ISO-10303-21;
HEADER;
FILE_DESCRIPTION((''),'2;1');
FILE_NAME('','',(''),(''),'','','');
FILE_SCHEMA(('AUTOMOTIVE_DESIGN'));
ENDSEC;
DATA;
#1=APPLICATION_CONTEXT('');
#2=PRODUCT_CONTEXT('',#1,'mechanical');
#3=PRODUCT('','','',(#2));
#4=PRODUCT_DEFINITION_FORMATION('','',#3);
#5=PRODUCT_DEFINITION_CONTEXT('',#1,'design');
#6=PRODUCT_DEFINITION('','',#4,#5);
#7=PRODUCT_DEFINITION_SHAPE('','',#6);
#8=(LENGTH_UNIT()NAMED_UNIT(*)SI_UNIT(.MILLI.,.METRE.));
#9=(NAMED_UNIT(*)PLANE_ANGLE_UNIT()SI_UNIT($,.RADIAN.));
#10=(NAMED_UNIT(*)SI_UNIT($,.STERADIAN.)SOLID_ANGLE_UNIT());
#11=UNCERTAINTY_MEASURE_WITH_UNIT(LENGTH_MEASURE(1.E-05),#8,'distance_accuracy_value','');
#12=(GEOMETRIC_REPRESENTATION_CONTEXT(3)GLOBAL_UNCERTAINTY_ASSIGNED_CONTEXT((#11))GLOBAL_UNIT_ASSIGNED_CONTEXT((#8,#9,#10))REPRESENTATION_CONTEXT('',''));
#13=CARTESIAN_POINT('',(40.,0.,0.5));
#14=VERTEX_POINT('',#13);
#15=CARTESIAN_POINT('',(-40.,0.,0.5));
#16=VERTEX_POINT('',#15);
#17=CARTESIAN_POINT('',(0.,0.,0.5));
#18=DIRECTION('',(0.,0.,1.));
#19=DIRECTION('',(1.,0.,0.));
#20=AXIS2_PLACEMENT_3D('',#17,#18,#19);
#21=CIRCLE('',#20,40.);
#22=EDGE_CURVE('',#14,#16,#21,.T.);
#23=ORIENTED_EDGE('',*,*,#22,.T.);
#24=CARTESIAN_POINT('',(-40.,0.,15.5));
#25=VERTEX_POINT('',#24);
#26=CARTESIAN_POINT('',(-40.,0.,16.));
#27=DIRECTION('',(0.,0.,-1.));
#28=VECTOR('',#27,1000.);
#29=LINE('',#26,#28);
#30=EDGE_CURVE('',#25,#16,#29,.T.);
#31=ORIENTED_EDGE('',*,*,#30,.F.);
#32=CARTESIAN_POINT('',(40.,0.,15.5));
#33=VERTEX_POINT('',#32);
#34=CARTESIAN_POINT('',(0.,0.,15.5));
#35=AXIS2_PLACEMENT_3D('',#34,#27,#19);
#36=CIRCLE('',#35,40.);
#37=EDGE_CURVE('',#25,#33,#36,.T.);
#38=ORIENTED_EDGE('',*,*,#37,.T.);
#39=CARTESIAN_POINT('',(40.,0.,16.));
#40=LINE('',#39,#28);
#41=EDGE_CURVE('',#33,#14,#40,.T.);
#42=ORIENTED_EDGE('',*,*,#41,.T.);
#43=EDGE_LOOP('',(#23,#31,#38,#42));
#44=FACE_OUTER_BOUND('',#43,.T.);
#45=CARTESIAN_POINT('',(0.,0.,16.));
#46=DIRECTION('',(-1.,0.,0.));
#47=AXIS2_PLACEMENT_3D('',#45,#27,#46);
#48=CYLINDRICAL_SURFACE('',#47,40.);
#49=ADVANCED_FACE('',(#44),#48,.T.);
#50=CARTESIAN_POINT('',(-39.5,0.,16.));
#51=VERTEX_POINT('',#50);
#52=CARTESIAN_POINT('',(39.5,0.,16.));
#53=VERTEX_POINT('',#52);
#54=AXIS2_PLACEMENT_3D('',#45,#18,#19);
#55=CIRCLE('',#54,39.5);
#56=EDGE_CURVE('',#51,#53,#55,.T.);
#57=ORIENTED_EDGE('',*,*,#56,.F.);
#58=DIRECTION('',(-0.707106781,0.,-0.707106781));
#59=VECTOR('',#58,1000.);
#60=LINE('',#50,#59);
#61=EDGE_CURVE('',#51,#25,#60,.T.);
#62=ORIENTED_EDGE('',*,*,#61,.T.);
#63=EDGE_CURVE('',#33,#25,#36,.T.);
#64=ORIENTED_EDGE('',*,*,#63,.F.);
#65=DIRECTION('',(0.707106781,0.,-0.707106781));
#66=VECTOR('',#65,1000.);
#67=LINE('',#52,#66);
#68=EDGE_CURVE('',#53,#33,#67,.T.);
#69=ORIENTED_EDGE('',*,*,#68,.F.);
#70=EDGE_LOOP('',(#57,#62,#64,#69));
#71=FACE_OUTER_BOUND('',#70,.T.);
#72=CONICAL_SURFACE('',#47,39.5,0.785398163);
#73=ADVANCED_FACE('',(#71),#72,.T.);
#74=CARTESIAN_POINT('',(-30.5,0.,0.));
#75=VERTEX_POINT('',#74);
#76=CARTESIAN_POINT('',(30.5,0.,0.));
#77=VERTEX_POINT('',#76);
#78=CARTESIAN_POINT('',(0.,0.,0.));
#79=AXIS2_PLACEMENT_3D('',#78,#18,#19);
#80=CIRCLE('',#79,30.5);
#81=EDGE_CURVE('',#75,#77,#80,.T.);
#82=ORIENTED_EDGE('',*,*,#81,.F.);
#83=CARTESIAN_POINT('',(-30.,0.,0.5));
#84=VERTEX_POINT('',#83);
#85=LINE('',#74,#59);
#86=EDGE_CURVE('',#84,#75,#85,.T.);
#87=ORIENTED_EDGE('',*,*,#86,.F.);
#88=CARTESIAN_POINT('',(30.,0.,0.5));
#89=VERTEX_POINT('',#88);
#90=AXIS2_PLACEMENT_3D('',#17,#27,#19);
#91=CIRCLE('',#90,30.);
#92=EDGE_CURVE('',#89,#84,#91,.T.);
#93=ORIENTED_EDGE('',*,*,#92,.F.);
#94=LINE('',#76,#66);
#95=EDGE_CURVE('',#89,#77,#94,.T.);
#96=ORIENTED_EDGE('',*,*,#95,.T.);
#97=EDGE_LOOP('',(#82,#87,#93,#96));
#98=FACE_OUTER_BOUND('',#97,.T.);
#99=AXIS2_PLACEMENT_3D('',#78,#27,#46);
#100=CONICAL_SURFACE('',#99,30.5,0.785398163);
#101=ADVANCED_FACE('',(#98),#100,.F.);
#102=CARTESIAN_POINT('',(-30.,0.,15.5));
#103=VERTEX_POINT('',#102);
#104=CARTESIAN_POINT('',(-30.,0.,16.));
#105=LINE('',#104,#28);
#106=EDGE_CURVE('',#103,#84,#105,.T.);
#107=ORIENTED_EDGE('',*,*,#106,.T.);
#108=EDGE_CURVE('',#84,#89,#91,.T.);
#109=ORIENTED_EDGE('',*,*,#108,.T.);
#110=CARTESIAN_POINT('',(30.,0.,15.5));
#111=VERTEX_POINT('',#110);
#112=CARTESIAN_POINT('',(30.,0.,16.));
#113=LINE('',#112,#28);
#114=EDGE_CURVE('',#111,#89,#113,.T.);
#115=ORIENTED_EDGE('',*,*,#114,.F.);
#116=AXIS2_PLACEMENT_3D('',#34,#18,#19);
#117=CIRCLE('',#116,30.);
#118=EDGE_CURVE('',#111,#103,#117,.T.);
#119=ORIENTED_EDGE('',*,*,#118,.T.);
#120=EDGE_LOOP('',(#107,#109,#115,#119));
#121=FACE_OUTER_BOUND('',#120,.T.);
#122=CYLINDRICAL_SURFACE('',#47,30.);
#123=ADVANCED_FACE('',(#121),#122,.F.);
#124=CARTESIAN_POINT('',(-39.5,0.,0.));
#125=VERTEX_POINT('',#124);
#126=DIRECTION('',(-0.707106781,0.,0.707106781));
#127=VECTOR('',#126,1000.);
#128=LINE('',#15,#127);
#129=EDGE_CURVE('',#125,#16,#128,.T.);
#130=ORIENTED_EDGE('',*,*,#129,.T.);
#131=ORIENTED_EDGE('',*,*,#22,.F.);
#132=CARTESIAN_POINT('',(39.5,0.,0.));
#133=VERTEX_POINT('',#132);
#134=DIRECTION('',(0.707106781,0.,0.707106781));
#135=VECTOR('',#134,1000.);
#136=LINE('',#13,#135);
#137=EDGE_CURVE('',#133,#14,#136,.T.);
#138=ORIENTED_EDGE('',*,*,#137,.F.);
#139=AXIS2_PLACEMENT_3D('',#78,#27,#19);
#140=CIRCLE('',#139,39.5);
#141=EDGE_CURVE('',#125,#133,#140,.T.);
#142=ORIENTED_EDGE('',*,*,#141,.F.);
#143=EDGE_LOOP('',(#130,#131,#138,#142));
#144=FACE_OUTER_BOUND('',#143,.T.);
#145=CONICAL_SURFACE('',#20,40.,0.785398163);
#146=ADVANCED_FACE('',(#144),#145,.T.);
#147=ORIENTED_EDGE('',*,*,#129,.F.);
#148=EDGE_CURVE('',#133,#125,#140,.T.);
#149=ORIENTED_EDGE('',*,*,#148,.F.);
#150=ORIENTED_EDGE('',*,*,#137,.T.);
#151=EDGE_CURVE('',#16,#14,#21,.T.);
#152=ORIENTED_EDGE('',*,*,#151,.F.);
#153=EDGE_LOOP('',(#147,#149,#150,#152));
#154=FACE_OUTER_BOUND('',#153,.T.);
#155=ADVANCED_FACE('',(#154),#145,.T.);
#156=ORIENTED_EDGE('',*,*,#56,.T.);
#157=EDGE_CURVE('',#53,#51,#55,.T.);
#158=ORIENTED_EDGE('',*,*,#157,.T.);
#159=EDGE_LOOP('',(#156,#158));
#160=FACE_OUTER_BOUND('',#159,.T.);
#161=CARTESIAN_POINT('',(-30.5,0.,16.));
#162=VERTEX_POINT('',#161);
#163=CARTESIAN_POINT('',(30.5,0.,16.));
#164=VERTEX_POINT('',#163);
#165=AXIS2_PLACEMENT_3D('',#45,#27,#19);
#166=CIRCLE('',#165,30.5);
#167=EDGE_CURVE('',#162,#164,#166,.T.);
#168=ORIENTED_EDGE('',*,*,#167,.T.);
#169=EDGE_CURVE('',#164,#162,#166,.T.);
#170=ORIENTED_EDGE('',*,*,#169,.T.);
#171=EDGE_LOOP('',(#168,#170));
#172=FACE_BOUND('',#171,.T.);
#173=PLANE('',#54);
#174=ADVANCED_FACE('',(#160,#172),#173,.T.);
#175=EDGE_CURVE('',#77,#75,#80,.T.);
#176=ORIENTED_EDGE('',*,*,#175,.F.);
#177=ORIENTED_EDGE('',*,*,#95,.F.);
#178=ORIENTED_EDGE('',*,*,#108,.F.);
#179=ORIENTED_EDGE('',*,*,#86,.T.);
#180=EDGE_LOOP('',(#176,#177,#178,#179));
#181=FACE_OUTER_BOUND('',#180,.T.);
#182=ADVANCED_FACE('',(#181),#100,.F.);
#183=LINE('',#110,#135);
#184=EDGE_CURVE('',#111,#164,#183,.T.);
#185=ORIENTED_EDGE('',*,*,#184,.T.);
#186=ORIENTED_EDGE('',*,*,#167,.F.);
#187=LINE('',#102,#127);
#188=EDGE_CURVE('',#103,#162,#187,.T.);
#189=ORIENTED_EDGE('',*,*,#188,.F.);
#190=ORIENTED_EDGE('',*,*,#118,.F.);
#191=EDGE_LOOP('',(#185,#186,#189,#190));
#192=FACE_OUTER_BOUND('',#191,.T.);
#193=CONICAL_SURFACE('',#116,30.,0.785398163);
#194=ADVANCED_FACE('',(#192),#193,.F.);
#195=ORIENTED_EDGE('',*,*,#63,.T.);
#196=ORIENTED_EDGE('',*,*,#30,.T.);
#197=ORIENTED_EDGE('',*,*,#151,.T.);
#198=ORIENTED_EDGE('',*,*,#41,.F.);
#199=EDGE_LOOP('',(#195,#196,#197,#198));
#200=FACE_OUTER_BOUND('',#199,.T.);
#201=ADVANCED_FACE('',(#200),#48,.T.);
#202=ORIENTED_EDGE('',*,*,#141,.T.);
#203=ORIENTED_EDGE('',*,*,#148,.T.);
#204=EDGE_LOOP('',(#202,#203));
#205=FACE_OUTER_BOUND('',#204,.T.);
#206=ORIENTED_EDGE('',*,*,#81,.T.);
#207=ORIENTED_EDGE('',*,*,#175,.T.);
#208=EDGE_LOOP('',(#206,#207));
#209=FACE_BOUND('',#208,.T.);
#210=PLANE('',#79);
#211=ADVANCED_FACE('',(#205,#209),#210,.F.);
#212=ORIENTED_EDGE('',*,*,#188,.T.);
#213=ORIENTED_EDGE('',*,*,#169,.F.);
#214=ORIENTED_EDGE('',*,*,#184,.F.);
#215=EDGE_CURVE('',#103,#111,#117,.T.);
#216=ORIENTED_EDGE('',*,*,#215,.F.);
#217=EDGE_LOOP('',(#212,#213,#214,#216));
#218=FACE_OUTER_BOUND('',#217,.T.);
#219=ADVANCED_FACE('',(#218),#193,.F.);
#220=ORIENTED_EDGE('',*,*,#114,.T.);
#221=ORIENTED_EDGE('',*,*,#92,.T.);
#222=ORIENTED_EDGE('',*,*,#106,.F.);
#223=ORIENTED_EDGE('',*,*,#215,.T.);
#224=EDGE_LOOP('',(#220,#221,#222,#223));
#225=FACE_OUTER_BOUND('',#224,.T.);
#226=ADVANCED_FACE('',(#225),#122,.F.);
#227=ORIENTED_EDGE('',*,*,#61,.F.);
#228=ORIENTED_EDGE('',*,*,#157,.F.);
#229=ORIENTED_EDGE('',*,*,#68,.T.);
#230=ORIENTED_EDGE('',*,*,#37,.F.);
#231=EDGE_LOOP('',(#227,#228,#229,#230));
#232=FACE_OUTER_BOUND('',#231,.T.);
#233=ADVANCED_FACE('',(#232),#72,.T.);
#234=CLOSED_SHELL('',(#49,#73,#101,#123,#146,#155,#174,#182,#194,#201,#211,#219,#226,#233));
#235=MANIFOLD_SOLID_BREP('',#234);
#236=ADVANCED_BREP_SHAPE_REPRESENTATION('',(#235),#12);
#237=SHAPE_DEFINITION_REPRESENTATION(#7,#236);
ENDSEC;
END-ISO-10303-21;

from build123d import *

# Parameters (mm, degrees)
SKETCH1_R           = 40
SKETCH1_R_2         = 30
BOSS_EXTRUDE1_DEPTH = 16
CHAMFER1_SIZE       = 0.5


with BuildPart() as part:
    # Sketch1 → Boss-Extrude1 (new body)
    with BuildSketch(Plane.XY):
        Circle(SKETCH1_R)
        Circle(SKETCH1_R_2, mode=Mode.SUBTRACT)
    extrude(amount=BOSS_EXTRUDE1_DEPTH)

    # Chamfer1
    chamfer1_edges = [part.edges().sort_by_distance(p)[0] for p in [
        (-40, 0, 0),
        (-40, 0, 16),
        (-30, 0, 0),
        (-30, 0, 16),
    ]]
    chamfer(chamfer1_edges, length=CHAMFER1_SIZE)


solid = part.part
